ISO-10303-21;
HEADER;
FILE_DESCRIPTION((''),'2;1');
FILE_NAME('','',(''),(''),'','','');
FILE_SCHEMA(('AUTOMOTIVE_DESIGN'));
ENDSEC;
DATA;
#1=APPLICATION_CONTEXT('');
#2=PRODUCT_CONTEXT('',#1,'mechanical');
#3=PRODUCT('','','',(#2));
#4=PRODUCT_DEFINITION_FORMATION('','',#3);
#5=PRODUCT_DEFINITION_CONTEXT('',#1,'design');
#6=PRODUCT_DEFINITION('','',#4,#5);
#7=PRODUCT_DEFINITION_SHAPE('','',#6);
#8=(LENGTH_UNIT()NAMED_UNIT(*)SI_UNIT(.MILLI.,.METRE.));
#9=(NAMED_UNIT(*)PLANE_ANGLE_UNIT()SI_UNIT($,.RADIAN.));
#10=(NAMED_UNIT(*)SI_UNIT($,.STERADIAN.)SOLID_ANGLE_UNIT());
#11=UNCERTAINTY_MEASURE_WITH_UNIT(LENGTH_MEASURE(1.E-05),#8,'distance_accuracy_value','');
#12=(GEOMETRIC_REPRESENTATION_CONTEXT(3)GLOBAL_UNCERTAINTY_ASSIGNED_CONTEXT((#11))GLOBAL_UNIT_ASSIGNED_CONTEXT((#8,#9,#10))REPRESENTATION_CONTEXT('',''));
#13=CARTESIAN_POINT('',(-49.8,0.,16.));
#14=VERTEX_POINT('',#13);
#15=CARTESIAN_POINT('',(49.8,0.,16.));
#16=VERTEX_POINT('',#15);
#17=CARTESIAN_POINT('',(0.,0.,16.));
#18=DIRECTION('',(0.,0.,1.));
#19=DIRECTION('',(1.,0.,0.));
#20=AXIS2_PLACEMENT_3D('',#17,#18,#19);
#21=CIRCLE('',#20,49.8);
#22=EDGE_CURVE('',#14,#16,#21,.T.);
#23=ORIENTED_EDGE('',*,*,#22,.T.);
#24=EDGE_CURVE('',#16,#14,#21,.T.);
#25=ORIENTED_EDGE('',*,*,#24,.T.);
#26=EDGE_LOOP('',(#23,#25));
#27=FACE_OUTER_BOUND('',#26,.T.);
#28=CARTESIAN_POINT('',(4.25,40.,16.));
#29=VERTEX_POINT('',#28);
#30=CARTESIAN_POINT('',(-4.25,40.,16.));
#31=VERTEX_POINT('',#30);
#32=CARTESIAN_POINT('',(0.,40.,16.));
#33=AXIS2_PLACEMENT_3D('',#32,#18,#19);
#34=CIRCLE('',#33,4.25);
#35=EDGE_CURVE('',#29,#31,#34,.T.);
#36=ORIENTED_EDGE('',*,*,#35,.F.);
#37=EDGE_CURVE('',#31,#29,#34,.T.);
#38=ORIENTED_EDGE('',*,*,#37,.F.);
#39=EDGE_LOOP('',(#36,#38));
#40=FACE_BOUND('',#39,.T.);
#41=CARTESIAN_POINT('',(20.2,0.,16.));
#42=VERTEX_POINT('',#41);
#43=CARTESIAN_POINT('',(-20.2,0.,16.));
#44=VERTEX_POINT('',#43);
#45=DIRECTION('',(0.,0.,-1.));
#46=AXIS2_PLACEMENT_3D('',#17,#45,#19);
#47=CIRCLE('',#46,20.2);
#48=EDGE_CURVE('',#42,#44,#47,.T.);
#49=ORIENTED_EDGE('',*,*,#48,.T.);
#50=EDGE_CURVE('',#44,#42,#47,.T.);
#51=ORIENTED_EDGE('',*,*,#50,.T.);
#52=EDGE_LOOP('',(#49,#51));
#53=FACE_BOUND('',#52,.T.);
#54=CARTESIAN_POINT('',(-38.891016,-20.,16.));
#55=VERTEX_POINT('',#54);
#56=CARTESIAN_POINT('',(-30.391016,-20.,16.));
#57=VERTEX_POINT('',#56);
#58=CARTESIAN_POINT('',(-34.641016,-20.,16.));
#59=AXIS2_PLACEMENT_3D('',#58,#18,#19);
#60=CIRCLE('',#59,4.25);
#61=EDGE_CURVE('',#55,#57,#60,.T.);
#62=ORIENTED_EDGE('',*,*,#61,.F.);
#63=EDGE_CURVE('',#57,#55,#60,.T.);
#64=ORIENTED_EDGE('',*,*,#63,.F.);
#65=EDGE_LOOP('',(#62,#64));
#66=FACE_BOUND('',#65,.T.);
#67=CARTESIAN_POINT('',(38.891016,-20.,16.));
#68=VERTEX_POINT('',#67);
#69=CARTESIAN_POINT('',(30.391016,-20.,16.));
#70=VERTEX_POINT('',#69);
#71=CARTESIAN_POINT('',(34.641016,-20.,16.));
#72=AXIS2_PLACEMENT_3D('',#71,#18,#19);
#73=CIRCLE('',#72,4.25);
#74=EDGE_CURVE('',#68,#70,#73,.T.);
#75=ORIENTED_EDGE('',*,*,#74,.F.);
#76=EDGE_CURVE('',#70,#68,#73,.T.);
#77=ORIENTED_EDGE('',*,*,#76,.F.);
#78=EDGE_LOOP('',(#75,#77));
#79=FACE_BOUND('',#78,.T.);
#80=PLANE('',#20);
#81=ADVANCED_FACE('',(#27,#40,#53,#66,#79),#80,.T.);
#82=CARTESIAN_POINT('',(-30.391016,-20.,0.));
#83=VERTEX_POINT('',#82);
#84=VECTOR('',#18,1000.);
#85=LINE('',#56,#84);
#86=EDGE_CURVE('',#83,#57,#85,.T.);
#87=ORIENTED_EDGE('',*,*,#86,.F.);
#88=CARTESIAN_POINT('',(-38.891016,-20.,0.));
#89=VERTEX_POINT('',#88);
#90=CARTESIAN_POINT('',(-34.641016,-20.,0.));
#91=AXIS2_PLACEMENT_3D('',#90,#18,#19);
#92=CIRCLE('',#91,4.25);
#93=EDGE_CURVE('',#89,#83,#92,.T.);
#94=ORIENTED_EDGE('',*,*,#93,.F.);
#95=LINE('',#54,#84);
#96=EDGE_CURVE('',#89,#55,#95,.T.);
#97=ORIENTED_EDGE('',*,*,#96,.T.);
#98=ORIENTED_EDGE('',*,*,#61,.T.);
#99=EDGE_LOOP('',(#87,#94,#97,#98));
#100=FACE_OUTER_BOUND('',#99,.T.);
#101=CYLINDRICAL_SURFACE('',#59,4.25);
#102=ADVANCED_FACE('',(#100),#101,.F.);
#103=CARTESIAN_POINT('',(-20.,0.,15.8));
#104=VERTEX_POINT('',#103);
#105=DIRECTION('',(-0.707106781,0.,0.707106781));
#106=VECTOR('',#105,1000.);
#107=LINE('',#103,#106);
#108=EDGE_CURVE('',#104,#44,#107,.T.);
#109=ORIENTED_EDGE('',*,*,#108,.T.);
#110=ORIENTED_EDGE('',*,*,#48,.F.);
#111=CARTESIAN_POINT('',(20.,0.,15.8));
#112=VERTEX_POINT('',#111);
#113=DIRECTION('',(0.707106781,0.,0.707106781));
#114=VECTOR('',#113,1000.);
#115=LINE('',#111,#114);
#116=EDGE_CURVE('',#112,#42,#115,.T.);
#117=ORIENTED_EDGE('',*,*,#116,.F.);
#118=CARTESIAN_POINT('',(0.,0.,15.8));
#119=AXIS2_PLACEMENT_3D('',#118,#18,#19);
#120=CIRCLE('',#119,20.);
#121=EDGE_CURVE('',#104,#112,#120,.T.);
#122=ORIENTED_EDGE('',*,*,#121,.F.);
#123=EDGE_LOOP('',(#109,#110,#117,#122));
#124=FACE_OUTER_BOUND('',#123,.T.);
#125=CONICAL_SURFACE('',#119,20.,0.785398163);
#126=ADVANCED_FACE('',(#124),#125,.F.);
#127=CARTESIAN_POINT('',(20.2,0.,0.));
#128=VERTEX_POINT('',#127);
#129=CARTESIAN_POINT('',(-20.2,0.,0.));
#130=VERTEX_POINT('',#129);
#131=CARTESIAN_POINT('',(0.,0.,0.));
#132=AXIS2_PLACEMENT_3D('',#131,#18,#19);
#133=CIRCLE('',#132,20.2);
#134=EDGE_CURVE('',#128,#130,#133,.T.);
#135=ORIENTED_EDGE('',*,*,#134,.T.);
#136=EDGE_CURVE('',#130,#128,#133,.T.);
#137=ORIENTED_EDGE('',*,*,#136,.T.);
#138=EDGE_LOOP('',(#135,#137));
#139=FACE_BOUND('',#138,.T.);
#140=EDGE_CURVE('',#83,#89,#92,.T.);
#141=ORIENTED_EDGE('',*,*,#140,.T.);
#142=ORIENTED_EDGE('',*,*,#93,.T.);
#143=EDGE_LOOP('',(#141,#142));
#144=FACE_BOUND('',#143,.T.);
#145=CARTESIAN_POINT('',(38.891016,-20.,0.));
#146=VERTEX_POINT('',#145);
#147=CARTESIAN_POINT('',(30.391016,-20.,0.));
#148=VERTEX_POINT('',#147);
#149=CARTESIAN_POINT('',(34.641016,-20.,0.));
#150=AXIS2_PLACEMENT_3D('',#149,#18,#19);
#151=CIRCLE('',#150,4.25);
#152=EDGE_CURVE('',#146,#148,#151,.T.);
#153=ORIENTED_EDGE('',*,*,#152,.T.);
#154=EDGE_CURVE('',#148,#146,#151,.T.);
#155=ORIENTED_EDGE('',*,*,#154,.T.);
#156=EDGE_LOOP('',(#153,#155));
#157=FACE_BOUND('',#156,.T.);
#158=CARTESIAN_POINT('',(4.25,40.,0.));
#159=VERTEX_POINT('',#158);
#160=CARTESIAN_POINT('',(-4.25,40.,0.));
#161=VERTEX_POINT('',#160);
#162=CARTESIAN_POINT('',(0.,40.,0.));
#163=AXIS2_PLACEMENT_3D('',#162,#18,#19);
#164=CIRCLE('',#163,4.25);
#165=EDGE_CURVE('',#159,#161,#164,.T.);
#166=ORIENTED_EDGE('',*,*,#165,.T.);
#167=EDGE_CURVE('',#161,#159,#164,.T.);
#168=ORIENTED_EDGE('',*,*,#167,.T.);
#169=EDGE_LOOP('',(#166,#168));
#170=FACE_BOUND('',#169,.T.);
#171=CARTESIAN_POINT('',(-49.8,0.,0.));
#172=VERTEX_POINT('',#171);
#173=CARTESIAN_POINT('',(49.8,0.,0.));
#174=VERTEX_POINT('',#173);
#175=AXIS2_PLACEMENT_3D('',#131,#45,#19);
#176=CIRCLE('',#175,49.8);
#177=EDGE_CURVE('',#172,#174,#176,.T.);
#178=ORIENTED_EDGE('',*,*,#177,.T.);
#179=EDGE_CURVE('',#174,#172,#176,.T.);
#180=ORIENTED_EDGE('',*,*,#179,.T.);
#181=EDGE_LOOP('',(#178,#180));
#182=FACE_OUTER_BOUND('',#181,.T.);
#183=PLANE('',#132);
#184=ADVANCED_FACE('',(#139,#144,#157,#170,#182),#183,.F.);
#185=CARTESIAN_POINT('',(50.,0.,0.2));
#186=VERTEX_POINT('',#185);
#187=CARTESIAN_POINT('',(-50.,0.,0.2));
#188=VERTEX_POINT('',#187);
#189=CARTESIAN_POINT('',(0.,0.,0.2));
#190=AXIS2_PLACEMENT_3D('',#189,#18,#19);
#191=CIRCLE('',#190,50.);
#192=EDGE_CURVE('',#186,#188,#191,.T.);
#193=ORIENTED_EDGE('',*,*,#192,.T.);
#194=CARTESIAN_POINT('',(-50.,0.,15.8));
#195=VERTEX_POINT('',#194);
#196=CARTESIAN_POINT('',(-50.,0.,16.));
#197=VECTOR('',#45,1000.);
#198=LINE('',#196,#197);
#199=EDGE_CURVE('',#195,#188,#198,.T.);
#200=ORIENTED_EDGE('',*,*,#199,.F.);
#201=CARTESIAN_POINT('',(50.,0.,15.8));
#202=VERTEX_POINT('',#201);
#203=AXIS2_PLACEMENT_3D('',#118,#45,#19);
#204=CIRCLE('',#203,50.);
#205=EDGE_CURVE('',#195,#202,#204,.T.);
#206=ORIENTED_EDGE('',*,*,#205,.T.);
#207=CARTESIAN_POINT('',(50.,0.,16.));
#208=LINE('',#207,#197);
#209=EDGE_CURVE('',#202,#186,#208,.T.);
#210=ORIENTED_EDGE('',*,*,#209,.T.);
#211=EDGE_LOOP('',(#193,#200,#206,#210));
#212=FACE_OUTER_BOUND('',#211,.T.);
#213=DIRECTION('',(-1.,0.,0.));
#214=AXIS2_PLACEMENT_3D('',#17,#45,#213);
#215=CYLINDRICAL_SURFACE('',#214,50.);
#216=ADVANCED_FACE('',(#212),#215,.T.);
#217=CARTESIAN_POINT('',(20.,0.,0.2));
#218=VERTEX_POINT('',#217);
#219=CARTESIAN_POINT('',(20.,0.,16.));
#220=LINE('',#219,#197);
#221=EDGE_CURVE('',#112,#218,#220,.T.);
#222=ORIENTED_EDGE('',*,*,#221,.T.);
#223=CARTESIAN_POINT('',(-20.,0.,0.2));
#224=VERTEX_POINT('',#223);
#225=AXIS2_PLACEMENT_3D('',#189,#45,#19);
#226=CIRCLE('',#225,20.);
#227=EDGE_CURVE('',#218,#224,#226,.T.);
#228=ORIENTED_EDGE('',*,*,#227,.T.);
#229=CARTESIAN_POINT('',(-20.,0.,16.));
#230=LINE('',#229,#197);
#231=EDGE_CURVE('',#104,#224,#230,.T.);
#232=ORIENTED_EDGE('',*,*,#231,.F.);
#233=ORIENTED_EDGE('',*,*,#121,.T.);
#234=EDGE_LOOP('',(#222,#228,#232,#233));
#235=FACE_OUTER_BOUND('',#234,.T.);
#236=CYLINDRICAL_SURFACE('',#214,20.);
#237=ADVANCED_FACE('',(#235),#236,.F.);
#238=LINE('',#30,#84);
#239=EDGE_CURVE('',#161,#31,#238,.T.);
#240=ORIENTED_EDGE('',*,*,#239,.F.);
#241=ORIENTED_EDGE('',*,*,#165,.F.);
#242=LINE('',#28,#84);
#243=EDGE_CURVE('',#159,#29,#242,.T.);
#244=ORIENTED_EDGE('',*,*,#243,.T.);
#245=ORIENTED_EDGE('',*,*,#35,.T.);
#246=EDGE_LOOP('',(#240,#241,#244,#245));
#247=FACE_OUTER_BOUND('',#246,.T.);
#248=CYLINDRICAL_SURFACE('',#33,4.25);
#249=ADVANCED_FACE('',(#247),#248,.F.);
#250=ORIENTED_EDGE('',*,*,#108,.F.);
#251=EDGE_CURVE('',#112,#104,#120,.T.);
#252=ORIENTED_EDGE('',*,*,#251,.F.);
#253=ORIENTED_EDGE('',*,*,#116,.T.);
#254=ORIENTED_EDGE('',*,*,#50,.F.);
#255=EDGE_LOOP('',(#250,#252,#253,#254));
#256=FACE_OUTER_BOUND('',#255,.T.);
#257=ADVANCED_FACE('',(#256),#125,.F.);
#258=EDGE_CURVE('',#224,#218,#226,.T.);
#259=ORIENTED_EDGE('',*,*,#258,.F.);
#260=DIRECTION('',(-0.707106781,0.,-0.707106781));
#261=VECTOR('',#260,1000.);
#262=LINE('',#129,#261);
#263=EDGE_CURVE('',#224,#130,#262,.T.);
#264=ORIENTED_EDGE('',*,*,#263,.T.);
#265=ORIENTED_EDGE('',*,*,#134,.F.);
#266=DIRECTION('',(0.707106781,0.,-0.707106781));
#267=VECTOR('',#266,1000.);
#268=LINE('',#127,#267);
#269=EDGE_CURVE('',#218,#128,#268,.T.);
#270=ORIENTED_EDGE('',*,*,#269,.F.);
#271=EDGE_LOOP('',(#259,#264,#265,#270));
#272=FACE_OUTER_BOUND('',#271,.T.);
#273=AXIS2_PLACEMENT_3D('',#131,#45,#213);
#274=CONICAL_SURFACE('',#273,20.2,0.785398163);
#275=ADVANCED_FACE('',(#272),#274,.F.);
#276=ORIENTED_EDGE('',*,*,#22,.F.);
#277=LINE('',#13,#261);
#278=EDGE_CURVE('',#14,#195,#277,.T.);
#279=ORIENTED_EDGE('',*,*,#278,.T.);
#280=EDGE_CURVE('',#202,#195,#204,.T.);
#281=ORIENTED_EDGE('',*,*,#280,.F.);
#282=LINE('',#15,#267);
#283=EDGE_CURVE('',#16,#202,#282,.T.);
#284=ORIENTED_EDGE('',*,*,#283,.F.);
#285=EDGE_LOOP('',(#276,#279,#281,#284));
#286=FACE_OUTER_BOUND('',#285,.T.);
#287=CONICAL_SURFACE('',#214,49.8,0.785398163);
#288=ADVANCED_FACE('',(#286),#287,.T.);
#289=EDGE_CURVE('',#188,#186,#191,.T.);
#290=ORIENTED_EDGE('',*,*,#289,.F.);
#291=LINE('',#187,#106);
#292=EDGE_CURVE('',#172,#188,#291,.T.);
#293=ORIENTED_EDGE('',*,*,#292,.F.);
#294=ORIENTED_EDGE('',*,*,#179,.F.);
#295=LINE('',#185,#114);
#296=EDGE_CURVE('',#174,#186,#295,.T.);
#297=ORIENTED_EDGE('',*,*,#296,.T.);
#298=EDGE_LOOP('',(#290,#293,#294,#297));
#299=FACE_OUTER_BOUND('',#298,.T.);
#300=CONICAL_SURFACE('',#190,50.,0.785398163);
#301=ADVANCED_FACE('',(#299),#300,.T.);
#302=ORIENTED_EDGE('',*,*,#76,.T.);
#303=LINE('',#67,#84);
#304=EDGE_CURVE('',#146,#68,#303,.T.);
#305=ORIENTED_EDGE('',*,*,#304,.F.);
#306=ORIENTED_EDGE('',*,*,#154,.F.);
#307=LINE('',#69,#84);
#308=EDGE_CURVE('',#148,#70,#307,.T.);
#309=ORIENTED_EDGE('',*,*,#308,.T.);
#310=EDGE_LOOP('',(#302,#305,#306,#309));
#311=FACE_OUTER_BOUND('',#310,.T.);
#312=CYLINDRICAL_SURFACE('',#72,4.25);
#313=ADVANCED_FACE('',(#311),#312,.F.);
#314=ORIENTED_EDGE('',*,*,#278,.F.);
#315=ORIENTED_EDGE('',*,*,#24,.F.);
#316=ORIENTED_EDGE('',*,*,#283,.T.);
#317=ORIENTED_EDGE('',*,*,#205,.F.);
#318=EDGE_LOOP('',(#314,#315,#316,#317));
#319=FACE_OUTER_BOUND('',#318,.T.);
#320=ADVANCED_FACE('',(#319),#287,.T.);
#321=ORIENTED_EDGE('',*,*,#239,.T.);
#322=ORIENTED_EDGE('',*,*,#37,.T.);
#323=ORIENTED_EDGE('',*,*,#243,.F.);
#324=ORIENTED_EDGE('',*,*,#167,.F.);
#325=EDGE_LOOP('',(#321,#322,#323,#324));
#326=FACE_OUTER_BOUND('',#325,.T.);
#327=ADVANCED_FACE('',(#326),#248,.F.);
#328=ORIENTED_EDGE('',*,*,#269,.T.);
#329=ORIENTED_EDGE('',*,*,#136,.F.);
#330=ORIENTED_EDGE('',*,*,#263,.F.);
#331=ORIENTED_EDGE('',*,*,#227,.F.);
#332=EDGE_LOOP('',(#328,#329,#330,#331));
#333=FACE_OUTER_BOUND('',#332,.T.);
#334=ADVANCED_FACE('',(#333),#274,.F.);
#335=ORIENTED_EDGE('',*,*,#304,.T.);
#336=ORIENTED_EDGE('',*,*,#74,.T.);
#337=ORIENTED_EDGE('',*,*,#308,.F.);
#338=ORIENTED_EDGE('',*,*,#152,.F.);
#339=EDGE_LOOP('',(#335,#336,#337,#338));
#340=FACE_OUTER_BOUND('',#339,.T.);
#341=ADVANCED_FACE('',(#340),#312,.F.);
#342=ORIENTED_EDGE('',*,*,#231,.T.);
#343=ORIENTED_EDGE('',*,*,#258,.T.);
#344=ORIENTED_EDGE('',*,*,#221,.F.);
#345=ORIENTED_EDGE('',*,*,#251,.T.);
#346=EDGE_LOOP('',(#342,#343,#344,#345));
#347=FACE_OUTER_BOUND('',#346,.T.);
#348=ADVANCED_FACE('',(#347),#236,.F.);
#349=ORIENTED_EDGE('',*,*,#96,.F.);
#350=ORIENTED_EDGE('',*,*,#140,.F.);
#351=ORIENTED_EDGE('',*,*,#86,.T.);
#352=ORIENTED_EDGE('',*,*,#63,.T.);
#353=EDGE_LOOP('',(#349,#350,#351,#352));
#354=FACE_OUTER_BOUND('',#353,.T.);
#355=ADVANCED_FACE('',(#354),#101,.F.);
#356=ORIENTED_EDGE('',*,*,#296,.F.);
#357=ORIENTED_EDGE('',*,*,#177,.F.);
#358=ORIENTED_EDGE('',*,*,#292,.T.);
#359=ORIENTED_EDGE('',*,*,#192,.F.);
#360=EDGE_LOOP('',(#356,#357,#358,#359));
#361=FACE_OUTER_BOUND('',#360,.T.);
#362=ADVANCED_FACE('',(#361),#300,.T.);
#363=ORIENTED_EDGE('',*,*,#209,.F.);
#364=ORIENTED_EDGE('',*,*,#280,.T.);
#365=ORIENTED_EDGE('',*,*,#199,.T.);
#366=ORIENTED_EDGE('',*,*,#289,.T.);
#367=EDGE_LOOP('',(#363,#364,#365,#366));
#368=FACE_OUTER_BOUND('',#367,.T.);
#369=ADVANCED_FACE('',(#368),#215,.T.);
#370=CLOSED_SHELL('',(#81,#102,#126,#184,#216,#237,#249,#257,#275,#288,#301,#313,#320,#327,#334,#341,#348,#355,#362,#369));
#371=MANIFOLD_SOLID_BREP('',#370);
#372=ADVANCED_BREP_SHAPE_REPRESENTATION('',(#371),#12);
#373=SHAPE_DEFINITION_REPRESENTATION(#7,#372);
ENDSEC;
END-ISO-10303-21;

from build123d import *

# Parameters (mm, degrees)
SKETCH1_R           = 50
SKETCH1_R_2         = 20
BOSS_EXTRUDE1_DEPTH = 16
CIRPATTERN1_COUNT   = 3
CHAMFER1_SIZE       = 0.2


with BuildPart() as part:
    # Sketch1 → Boss-Extrude1 (new body)
    with BuildSketch(Plane.XY):
        Circle(SKETCH1_R)
        Circle(SKETCH1_R_2, mode=Mode.SUBTRACT)
    extrude(amount=BOSS_EXTRUDE1_DEPTH)

    # Sketch5 → M10 Tapped Hole1 (revolve, cut)
    with BuildSketch(Plane(origin=(0, 40, 16), x_dir=(0, -1, 0), z_dir=(1, 0, 0))):
        Polygon((0, 0), (0, 31.803657631), (4.25, 29.25), (4.25, 0), align=None)
    m10_tapped_hole1 = revolve(axis=Axis((0, 40, 22.35), (0, 0, -1)), mode=Mode.SUBTRACT)

    # CirPattern1: M10 Tapped Hole1 ×3 about axis
    cirpattern1_axis = Axis((0, 0, 0), (0, 0, 1))
    for i in range(1, CIRPATTERN1_COUNT):
        add(m10_tapped_hole1.rotate(cirpattern1_axis, i * 360 / CIRPATTERN1_COUNT), mode=Mode.SUBTRACT)

    # Chamfer1
    chamfer1_edges = [part.edges().sort_by_distance(p)[0] for p in [
        (-50, 0, 0),
        (-50, 0, 16),
        (-20, 0, 0),
        (-20, 0, 16),
    ]]
    chamfer(chamfer1_edges, length=CHAMFER1_SIZE)


solid = part.part
